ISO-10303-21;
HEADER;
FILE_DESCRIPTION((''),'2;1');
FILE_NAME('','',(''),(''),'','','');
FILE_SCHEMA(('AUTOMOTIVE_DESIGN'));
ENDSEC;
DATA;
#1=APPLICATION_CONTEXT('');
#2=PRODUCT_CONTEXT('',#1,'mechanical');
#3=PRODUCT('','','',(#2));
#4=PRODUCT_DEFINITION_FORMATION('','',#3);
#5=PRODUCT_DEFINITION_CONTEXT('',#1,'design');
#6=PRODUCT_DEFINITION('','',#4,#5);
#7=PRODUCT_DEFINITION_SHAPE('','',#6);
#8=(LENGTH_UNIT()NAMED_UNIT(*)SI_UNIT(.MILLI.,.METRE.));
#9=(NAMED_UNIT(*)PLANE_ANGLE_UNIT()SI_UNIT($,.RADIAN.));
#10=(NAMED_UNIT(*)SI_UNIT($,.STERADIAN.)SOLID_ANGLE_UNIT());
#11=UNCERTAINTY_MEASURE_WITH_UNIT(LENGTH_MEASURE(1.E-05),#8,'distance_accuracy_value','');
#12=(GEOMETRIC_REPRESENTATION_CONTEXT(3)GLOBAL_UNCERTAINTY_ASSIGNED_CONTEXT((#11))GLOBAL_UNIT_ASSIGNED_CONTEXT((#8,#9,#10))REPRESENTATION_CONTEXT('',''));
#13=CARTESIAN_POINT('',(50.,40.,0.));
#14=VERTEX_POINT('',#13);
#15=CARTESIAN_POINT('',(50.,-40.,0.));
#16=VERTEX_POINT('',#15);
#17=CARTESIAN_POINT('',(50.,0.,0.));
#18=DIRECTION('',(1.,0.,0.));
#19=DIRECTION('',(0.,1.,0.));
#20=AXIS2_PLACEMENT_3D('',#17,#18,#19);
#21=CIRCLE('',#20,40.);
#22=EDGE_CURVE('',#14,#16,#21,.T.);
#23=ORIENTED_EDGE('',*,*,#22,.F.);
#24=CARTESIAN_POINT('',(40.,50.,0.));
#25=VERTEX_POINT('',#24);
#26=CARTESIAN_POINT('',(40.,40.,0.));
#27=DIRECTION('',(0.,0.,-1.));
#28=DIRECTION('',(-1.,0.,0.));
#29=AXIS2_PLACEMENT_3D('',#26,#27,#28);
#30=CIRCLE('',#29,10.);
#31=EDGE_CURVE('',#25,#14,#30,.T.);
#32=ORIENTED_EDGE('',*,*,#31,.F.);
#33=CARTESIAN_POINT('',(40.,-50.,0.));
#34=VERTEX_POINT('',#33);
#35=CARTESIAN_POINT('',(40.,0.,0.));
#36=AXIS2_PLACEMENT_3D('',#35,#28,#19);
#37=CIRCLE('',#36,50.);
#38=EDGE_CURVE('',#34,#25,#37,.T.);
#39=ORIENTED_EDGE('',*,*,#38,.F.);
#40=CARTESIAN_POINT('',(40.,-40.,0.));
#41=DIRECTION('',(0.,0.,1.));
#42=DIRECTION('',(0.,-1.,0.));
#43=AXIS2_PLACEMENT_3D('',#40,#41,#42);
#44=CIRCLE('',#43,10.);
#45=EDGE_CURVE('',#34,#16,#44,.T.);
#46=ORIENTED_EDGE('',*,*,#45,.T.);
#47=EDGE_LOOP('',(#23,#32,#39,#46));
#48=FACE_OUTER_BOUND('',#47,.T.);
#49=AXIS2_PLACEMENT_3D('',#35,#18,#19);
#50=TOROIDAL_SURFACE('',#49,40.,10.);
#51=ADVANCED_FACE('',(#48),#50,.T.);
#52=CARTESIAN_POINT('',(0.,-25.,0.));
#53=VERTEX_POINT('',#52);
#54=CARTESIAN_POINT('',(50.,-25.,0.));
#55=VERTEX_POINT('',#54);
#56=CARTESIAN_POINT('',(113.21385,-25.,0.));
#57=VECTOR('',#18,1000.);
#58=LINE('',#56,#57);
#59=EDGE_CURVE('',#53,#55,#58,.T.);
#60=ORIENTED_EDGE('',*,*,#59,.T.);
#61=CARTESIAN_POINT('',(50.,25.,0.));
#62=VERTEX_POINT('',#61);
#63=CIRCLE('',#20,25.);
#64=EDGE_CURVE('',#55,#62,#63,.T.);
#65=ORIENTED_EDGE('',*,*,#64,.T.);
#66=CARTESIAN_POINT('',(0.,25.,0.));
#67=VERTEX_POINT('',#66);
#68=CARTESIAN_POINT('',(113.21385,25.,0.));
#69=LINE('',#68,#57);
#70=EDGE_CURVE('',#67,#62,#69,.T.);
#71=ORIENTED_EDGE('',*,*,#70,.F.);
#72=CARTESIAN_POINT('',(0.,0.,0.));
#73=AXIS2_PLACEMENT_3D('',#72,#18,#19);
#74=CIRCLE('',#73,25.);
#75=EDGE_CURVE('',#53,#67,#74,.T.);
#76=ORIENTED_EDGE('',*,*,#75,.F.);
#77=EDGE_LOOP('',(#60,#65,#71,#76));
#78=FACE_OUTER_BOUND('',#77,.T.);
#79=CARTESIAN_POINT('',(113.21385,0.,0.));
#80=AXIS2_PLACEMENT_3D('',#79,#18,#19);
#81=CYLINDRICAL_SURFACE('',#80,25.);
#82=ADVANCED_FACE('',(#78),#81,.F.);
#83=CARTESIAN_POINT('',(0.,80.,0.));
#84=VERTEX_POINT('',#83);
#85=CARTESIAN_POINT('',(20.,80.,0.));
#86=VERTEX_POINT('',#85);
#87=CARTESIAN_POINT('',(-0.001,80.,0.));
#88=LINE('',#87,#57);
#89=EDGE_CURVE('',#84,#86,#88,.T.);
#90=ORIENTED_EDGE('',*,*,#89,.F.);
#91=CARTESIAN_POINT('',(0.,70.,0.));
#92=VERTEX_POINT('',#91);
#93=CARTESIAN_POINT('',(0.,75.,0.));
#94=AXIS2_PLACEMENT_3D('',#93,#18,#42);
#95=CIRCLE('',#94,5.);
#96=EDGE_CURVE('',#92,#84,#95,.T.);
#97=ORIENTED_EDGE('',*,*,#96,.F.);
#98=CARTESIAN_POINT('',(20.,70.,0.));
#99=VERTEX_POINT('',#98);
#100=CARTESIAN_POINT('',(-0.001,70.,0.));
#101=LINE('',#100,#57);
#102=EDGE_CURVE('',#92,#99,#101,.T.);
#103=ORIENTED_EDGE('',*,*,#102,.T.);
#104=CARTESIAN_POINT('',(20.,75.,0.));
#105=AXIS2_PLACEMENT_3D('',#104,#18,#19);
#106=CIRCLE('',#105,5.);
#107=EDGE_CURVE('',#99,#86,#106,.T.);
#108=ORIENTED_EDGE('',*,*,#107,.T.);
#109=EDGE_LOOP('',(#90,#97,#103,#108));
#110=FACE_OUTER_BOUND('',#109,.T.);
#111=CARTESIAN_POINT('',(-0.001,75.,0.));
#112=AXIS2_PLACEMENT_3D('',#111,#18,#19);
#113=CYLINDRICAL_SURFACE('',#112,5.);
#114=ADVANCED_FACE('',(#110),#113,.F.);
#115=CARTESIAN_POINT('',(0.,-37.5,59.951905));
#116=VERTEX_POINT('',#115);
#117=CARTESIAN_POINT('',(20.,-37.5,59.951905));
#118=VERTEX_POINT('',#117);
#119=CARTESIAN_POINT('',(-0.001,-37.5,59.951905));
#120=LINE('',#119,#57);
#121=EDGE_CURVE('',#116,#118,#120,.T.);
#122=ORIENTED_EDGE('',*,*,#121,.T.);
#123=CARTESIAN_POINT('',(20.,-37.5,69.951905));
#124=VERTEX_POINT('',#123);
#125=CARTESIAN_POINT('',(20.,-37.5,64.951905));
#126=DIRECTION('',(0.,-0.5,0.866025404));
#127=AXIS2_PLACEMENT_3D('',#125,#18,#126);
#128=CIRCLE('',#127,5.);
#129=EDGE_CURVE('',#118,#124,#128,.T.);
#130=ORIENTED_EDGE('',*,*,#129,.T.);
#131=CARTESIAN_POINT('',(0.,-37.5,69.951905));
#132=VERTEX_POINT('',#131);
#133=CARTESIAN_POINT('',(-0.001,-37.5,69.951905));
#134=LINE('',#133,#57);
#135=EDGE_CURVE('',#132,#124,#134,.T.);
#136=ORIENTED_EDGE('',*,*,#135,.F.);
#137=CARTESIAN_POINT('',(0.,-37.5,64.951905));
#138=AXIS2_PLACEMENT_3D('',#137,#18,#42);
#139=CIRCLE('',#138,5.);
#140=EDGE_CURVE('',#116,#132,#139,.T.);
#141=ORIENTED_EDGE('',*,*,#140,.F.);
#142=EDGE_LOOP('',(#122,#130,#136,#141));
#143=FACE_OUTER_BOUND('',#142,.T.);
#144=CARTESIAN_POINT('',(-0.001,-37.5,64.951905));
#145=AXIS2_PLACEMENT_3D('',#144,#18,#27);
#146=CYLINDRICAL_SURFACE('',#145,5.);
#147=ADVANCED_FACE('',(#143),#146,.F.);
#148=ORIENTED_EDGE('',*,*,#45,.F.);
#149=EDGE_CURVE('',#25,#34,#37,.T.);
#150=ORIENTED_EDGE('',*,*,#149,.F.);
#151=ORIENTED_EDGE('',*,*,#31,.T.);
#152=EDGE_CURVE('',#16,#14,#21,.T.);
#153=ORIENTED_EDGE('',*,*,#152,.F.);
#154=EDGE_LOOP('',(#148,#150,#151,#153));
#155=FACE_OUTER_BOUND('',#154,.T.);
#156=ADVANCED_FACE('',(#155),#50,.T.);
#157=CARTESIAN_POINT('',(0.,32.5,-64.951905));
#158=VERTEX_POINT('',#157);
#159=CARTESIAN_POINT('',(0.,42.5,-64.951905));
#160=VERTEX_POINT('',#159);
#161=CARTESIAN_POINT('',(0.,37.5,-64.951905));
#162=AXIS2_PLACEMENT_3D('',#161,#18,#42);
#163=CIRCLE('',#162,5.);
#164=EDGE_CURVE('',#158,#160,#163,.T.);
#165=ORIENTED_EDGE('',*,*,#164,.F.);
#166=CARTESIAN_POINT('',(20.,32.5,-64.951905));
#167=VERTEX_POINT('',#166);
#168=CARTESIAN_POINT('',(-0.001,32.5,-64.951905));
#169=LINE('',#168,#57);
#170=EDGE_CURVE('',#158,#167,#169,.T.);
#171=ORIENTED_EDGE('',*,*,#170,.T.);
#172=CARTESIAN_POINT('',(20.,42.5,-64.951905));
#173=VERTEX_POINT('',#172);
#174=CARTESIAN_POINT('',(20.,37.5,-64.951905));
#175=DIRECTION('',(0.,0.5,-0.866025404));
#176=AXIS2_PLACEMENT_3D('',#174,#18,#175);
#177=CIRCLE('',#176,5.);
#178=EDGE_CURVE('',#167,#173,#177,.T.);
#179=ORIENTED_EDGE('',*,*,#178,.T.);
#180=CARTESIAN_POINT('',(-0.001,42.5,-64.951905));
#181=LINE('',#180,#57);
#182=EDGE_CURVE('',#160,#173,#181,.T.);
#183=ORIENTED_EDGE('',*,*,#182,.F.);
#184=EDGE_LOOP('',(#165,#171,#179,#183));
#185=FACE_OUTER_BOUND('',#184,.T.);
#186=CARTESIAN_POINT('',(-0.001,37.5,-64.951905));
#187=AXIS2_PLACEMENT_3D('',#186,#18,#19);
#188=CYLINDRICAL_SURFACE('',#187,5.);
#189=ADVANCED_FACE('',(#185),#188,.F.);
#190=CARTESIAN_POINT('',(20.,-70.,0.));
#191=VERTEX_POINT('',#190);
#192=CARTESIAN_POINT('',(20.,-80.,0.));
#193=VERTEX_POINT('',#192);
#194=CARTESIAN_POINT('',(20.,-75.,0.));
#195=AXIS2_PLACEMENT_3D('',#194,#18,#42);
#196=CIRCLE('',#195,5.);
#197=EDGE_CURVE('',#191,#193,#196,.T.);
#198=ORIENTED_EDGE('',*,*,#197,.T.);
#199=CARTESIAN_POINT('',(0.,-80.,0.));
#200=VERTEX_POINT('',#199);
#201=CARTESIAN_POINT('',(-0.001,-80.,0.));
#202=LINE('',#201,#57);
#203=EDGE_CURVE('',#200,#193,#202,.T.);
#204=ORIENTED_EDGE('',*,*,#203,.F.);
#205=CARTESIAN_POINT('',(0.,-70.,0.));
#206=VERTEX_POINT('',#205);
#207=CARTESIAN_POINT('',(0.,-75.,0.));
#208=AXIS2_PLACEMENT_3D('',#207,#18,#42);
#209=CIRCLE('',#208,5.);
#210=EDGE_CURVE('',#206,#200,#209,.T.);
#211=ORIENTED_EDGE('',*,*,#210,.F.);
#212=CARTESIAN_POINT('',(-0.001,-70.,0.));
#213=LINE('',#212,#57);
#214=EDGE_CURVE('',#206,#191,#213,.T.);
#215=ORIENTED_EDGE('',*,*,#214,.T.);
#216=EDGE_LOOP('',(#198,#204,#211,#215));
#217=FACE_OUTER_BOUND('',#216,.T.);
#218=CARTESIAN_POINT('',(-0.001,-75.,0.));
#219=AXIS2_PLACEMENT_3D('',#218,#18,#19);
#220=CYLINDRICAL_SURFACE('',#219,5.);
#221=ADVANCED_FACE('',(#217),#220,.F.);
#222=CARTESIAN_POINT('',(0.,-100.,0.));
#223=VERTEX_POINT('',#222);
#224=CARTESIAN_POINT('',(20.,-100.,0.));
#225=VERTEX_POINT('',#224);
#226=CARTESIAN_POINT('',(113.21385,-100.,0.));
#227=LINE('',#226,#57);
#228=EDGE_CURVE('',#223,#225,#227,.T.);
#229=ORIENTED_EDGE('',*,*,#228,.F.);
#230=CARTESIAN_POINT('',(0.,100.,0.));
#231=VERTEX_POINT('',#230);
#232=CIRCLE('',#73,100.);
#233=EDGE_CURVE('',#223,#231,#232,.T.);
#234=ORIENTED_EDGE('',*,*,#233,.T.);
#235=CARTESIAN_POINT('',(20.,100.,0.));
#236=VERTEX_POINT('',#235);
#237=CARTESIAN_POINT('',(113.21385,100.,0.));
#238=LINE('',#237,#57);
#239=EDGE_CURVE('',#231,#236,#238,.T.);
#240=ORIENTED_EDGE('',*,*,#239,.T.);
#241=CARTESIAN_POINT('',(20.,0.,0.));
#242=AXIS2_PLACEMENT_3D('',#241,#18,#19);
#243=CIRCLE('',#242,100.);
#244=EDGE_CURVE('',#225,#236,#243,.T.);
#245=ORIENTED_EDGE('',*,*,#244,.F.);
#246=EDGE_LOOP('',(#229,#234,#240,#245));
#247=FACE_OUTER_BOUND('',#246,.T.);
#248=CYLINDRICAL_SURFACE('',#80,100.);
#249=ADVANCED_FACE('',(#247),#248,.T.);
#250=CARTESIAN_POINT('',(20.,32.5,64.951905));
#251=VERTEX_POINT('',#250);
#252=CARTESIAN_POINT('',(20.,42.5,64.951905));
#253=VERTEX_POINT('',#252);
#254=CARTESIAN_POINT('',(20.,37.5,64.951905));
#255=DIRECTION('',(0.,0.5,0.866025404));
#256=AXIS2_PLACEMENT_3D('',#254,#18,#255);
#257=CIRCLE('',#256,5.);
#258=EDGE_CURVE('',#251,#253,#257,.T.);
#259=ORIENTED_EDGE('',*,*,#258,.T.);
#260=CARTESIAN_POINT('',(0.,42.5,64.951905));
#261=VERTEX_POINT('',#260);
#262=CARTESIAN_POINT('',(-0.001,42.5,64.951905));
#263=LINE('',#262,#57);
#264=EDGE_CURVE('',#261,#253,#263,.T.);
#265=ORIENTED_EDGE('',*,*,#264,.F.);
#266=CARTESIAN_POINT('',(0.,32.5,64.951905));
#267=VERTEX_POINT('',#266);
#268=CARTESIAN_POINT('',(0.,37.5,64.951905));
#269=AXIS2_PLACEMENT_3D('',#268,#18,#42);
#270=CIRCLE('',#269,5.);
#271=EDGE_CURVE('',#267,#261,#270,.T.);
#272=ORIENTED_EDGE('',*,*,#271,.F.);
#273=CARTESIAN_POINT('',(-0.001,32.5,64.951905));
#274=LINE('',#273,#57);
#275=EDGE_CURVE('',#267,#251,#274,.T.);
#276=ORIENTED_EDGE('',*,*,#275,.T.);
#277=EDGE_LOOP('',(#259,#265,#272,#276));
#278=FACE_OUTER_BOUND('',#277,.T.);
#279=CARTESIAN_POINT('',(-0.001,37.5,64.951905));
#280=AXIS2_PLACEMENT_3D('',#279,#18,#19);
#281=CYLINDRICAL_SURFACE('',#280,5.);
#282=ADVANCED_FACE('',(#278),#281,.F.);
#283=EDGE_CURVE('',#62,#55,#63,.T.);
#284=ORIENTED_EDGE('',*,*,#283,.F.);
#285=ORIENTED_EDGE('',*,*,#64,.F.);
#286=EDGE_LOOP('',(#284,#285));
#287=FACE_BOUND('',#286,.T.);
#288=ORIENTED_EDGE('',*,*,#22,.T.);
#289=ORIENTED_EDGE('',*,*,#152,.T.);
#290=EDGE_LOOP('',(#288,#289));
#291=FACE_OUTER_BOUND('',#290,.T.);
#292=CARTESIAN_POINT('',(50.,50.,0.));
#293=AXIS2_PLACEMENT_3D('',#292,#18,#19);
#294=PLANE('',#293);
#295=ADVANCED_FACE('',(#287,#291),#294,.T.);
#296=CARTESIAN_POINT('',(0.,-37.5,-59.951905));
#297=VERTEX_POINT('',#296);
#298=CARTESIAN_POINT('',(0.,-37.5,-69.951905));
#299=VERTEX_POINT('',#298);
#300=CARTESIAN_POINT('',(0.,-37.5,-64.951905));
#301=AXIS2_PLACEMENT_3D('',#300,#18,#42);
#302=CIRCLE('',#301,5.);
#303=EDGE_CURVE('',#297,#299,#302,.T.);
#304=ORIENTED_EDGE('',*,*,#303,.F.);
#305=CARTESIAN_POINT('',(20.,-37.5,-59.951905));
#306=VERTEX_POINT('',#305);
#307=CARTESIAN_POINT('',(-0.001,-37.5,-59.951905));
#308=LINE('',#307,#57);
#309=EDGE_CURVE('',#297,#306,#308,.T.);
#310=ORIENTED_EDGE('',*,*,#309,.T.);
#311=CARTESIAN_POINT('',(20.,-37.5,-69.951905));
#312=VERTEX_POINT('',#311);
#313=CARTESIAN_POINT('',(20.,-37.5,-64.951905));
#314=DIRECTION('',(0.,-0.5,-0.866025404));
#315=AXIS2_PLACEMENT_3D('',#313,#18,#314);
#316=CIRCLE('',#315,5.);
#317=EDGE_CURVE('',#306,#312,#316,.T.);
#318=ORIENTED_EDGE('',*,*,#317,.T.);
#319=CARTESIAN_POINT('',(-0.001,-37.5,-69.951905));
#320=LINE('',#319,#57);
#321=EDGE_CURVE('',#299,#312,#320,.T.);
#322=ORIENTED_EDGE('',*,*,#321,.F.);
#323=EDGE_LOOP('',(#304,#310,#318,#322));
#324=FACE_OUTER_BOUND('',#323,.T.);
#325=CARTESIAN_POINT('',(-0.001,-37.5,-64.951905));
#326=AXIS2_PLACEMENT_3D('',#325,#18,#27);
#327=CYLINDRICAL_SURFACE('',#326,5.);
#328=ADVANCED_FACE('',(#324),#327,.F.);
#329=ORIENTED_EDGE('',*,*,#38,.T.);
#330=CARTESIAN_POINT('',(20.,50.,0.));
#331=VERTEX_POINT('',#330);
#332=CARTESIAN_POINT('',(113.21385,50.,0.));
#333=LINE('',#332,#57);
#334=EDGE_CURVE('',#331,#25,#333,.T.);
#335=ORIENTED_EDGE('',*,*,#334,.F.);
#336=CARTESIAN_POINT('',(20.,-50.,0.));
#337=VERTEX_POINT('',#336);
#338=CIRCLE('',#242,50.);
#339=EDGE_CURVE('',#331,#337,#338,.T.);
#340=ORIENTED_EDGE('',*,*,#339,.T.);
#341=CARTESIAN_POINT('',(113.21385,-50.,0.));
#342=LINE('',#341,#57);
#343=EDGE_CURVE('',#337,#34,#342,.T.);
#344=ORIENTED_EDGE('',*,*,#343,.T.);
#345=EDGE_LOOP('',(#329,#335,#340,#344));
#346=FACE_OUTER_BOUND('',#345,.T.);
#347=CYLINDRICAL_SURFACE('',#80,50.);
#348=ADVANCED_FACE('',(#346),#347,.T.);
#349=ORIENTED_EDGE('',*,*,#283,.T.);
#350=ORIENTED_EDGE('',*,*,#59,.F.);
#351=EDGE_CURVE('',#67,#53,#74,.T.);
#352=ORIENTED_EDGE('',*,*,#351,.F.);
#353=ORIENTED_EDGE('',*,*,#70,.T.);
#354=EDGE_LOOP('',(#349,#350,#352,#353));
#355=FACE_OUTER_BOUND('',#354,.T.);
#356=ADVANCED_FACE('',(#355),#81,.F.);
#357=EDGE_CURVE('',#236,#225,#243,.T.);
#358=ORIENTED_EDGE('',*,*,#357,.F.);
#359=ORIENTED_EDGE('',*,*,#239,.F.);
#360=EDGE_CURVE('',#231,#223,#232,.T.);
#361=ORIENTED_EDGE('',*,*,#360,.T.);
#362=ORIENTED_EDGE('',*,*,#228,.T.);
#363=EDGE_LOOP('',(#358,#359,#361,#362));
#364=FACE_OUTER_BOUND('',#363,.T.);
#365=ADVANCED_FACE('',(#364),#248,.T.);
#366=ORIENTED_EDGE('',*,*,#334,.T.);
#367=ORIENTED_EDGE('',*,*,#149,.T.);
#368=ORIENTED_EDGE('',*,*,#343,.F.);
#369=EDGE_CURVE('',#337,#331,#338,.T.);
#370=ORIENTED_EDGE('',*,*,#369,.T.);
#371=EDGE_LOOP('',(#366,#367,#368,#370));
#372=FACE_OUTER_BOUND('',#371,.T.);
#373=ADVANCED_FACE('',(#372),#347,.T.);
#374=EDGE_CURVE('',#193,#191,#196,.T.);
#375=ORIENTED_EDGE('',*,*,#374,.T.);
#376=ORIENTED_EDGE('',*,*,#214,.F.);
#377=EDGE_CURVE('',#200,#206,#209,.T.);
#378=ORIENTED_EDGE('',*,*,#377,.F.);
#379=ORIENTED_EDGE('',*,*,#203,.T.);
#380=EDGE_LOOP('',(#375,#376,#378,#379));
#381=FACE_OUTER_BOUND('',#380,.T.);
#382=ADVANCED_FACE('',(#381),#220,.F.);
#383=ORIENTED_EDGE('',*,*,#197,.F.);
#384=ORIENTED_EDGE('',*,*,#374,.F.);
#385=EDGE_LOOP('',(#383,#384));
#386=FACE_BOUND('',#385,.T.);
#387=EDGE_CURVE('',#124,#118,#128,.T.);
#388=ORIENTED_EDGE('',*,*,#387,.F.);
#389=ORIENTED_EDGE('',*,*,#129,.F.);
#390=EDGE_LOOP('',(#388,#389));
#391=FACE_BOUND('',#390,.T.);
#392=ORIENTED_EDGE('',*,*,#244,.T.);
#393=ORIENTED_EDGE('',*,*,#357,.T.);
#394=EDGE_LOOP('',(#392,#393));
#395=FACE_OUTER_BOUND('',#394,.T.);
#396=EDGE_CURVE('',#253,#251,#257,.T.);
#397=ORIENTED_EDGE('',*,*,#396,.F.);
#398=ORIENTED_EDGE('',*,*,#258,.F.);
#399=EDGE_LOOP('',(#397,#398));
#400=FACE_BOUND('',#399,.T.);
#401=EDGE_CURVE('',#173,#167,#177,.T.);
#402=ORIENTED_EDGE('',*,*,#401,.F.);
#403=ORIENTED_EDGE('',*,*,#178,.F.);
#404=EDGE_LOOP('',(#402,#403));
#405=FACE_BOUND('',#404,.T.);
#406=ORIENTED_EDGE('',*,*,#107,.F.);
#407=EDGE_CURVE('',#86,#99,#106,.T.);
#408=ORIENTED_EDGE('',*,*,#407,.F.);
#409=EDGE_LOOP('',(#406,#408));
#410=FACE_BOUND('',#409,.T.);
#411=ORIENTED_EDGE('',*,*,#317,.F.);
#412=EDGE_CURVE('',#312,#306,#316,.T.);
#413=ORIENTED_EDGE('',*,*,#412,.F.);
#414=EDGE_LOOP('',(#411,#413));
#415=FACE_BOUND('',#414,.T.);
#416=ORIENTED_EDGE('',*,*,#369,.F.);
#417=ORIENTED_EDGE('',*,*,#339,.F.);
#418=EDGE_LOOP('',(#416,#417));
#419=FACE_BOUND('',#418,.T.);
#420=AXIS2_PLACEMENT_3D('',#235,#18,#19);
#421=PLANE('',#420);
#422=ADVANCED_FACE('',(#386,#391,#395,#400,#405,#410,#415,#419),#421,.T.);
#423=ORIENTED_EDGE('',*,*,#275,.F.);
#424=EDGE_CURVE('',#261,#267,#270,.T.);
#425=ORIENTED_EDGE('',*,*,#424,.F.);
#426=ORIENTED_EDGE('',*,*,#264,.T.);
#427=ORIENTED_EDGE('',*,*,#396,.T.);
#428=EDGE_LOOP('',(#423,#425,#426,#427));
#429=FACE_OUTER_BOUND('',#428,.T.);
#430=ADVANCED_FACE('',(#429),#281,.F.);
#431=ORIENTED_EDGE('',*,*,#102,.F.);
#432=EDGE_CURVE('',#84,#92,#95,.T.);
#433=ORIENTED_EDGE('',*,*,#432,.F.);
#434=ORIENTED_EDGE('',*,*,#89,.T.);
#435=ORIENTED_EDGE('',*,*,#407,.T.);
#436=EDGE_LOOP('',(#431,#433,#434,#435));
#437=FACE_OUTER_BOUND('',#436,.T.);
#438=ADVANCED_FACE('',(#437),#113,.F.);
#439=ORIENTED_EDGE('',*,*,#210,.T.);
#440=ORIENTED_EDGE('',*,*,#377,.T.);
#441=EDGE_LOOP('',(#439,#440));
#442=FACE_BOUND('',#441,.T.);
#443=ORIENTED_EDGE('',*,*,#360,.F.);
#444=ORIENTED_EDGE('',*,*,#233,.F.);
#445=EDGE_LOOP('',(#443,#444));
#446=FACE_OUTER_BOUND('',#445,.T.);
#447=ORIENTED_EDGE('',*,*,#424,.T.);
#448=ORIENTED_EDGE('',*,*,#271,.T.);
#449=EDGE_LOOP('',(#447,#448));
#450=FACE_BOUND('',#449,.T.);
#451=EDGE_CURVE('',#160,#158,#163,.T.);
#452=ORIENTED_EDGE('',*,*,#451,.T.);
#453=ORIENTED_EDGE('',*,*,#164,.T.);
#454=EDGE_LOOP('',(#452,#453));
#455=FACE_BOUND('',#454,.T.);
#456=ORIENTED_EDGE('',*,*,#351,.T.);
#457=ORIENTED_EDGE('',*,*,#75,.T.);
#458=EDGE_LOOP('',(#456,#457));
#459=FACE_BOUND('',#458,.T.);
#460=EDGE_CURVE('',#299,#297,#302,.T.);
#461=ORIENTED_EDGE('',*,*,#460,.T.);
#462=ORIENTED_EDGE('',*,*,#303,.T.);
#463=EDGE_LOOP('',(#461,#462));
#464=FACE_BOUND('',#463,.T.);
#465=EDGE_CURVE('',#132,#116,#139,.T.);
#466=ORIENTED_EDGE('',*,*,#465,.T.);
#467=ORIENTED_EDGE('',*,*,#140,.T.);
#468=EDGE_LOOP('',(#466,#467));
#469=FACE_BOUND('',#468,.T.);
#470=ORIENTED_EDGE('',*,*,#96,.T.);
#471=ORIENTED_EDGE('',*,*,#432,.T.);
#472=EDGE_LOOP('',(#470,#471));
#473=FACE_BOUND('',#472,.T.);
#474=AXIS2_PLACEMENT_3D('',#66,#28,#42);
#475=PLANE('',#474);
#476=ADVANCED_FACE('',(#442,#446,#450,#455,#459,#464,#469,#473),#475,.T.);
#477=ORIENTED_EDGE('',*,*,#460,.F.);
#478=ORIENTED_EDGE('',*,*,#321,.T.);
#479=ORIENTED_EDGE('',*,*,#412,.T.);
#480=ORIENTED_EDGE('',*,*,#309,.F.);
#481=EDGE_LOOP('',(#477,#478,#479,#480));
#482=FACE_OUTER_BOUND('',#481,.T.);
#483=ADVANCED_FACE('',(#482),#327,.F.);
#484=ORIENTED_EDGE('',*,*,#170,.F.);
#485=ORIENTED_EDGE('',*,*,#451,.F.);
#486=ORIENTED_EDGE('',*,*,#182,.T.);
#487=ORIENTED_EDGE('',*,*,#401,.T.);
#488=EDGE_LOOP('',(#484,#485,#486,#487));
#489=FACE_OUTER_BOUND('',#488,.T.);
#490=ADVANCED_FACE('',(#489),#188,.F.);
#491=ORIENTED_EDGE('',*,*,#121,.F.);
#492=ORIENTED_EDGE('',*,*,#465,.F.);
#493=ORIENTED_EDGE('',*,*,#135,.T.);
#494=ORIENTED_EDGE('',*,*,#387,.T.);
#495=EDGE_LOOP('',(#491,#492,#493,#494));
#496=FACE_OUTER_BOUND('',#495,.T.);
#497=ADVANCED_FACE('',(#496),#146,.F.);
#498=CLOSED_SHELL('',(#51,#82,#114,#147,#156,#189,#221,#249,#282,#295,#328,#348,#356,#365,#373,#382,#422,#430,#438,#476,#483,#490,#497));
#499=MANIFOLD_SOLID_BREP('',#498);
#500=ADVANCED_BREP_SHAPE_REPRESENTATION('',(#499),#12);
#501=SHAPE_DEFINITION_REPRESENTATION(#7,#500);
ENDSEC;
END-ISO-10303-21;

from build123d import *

# Parameters (mm, degrees)
CUT_EXTRUDE1_REACH = 146.568
SKETCH3_R          = 5
CIRPATTERN1_COUNT  = 6
FILLET1_R          = 10


with BuildPart() as part:
    # Sketch1 → Revolve1 (revolve)
    with BuildSketch(Plane.XY):
        Polygon((0, 25), (0, 100), (20, 100), (20, 50), (50, 50), (50, 25), align=None)
    revolve(axis=Axis((113.213850314, 0, 0), (-1, 0, 0)))

    # Sketch3 → Cut-Extrude1 (cut, up to next)
    with BuildSketch(Plane(origin=(20, 0, 0), x_dir=(0, 0, -1), z_dir=(1, 0, 0)), mode=Mode.PRIVATE) as cut_extrude1_sk1:
        with Locations(Location((0, 75, 0), (0, 0, 90))):
            Circle(SKETCH3_R)
    cut_extrude1_tool1 = extrude(cut_extrude1_sk1.sketch, amount=-CUT_EXTRUDE1_REACH, mode=Mode.PRIVATE) & part.part
    cut_extrude1 = cut_extrude1_tool1.solids().sort_by_distance((20, 75, 0))[0]
    add(cut_extrude1, mode=Mode.SUBTRACT)

    # CirPattern1: Cut-Extrude1 ×6 about axis
    cirpattern1_axis = Axis((0, 0, 0), (1, 0, 0))
    for i in range(1, CIRPATTERN1_COUNT):
        add(cut_extrude1.rotate(cirpattern1_axis, i * 360 / CIRPATTERN1_COUNT), mode=Mode.SUBTRACT)

    # Fillet1
    fillet1_edges = [part.edges().sort_by_distance(p)[0] for p in [
        (50, -50, 0),
    ]]
    fillet(fillet1_edges, radius=FILLET1_R)


solid = part.part
